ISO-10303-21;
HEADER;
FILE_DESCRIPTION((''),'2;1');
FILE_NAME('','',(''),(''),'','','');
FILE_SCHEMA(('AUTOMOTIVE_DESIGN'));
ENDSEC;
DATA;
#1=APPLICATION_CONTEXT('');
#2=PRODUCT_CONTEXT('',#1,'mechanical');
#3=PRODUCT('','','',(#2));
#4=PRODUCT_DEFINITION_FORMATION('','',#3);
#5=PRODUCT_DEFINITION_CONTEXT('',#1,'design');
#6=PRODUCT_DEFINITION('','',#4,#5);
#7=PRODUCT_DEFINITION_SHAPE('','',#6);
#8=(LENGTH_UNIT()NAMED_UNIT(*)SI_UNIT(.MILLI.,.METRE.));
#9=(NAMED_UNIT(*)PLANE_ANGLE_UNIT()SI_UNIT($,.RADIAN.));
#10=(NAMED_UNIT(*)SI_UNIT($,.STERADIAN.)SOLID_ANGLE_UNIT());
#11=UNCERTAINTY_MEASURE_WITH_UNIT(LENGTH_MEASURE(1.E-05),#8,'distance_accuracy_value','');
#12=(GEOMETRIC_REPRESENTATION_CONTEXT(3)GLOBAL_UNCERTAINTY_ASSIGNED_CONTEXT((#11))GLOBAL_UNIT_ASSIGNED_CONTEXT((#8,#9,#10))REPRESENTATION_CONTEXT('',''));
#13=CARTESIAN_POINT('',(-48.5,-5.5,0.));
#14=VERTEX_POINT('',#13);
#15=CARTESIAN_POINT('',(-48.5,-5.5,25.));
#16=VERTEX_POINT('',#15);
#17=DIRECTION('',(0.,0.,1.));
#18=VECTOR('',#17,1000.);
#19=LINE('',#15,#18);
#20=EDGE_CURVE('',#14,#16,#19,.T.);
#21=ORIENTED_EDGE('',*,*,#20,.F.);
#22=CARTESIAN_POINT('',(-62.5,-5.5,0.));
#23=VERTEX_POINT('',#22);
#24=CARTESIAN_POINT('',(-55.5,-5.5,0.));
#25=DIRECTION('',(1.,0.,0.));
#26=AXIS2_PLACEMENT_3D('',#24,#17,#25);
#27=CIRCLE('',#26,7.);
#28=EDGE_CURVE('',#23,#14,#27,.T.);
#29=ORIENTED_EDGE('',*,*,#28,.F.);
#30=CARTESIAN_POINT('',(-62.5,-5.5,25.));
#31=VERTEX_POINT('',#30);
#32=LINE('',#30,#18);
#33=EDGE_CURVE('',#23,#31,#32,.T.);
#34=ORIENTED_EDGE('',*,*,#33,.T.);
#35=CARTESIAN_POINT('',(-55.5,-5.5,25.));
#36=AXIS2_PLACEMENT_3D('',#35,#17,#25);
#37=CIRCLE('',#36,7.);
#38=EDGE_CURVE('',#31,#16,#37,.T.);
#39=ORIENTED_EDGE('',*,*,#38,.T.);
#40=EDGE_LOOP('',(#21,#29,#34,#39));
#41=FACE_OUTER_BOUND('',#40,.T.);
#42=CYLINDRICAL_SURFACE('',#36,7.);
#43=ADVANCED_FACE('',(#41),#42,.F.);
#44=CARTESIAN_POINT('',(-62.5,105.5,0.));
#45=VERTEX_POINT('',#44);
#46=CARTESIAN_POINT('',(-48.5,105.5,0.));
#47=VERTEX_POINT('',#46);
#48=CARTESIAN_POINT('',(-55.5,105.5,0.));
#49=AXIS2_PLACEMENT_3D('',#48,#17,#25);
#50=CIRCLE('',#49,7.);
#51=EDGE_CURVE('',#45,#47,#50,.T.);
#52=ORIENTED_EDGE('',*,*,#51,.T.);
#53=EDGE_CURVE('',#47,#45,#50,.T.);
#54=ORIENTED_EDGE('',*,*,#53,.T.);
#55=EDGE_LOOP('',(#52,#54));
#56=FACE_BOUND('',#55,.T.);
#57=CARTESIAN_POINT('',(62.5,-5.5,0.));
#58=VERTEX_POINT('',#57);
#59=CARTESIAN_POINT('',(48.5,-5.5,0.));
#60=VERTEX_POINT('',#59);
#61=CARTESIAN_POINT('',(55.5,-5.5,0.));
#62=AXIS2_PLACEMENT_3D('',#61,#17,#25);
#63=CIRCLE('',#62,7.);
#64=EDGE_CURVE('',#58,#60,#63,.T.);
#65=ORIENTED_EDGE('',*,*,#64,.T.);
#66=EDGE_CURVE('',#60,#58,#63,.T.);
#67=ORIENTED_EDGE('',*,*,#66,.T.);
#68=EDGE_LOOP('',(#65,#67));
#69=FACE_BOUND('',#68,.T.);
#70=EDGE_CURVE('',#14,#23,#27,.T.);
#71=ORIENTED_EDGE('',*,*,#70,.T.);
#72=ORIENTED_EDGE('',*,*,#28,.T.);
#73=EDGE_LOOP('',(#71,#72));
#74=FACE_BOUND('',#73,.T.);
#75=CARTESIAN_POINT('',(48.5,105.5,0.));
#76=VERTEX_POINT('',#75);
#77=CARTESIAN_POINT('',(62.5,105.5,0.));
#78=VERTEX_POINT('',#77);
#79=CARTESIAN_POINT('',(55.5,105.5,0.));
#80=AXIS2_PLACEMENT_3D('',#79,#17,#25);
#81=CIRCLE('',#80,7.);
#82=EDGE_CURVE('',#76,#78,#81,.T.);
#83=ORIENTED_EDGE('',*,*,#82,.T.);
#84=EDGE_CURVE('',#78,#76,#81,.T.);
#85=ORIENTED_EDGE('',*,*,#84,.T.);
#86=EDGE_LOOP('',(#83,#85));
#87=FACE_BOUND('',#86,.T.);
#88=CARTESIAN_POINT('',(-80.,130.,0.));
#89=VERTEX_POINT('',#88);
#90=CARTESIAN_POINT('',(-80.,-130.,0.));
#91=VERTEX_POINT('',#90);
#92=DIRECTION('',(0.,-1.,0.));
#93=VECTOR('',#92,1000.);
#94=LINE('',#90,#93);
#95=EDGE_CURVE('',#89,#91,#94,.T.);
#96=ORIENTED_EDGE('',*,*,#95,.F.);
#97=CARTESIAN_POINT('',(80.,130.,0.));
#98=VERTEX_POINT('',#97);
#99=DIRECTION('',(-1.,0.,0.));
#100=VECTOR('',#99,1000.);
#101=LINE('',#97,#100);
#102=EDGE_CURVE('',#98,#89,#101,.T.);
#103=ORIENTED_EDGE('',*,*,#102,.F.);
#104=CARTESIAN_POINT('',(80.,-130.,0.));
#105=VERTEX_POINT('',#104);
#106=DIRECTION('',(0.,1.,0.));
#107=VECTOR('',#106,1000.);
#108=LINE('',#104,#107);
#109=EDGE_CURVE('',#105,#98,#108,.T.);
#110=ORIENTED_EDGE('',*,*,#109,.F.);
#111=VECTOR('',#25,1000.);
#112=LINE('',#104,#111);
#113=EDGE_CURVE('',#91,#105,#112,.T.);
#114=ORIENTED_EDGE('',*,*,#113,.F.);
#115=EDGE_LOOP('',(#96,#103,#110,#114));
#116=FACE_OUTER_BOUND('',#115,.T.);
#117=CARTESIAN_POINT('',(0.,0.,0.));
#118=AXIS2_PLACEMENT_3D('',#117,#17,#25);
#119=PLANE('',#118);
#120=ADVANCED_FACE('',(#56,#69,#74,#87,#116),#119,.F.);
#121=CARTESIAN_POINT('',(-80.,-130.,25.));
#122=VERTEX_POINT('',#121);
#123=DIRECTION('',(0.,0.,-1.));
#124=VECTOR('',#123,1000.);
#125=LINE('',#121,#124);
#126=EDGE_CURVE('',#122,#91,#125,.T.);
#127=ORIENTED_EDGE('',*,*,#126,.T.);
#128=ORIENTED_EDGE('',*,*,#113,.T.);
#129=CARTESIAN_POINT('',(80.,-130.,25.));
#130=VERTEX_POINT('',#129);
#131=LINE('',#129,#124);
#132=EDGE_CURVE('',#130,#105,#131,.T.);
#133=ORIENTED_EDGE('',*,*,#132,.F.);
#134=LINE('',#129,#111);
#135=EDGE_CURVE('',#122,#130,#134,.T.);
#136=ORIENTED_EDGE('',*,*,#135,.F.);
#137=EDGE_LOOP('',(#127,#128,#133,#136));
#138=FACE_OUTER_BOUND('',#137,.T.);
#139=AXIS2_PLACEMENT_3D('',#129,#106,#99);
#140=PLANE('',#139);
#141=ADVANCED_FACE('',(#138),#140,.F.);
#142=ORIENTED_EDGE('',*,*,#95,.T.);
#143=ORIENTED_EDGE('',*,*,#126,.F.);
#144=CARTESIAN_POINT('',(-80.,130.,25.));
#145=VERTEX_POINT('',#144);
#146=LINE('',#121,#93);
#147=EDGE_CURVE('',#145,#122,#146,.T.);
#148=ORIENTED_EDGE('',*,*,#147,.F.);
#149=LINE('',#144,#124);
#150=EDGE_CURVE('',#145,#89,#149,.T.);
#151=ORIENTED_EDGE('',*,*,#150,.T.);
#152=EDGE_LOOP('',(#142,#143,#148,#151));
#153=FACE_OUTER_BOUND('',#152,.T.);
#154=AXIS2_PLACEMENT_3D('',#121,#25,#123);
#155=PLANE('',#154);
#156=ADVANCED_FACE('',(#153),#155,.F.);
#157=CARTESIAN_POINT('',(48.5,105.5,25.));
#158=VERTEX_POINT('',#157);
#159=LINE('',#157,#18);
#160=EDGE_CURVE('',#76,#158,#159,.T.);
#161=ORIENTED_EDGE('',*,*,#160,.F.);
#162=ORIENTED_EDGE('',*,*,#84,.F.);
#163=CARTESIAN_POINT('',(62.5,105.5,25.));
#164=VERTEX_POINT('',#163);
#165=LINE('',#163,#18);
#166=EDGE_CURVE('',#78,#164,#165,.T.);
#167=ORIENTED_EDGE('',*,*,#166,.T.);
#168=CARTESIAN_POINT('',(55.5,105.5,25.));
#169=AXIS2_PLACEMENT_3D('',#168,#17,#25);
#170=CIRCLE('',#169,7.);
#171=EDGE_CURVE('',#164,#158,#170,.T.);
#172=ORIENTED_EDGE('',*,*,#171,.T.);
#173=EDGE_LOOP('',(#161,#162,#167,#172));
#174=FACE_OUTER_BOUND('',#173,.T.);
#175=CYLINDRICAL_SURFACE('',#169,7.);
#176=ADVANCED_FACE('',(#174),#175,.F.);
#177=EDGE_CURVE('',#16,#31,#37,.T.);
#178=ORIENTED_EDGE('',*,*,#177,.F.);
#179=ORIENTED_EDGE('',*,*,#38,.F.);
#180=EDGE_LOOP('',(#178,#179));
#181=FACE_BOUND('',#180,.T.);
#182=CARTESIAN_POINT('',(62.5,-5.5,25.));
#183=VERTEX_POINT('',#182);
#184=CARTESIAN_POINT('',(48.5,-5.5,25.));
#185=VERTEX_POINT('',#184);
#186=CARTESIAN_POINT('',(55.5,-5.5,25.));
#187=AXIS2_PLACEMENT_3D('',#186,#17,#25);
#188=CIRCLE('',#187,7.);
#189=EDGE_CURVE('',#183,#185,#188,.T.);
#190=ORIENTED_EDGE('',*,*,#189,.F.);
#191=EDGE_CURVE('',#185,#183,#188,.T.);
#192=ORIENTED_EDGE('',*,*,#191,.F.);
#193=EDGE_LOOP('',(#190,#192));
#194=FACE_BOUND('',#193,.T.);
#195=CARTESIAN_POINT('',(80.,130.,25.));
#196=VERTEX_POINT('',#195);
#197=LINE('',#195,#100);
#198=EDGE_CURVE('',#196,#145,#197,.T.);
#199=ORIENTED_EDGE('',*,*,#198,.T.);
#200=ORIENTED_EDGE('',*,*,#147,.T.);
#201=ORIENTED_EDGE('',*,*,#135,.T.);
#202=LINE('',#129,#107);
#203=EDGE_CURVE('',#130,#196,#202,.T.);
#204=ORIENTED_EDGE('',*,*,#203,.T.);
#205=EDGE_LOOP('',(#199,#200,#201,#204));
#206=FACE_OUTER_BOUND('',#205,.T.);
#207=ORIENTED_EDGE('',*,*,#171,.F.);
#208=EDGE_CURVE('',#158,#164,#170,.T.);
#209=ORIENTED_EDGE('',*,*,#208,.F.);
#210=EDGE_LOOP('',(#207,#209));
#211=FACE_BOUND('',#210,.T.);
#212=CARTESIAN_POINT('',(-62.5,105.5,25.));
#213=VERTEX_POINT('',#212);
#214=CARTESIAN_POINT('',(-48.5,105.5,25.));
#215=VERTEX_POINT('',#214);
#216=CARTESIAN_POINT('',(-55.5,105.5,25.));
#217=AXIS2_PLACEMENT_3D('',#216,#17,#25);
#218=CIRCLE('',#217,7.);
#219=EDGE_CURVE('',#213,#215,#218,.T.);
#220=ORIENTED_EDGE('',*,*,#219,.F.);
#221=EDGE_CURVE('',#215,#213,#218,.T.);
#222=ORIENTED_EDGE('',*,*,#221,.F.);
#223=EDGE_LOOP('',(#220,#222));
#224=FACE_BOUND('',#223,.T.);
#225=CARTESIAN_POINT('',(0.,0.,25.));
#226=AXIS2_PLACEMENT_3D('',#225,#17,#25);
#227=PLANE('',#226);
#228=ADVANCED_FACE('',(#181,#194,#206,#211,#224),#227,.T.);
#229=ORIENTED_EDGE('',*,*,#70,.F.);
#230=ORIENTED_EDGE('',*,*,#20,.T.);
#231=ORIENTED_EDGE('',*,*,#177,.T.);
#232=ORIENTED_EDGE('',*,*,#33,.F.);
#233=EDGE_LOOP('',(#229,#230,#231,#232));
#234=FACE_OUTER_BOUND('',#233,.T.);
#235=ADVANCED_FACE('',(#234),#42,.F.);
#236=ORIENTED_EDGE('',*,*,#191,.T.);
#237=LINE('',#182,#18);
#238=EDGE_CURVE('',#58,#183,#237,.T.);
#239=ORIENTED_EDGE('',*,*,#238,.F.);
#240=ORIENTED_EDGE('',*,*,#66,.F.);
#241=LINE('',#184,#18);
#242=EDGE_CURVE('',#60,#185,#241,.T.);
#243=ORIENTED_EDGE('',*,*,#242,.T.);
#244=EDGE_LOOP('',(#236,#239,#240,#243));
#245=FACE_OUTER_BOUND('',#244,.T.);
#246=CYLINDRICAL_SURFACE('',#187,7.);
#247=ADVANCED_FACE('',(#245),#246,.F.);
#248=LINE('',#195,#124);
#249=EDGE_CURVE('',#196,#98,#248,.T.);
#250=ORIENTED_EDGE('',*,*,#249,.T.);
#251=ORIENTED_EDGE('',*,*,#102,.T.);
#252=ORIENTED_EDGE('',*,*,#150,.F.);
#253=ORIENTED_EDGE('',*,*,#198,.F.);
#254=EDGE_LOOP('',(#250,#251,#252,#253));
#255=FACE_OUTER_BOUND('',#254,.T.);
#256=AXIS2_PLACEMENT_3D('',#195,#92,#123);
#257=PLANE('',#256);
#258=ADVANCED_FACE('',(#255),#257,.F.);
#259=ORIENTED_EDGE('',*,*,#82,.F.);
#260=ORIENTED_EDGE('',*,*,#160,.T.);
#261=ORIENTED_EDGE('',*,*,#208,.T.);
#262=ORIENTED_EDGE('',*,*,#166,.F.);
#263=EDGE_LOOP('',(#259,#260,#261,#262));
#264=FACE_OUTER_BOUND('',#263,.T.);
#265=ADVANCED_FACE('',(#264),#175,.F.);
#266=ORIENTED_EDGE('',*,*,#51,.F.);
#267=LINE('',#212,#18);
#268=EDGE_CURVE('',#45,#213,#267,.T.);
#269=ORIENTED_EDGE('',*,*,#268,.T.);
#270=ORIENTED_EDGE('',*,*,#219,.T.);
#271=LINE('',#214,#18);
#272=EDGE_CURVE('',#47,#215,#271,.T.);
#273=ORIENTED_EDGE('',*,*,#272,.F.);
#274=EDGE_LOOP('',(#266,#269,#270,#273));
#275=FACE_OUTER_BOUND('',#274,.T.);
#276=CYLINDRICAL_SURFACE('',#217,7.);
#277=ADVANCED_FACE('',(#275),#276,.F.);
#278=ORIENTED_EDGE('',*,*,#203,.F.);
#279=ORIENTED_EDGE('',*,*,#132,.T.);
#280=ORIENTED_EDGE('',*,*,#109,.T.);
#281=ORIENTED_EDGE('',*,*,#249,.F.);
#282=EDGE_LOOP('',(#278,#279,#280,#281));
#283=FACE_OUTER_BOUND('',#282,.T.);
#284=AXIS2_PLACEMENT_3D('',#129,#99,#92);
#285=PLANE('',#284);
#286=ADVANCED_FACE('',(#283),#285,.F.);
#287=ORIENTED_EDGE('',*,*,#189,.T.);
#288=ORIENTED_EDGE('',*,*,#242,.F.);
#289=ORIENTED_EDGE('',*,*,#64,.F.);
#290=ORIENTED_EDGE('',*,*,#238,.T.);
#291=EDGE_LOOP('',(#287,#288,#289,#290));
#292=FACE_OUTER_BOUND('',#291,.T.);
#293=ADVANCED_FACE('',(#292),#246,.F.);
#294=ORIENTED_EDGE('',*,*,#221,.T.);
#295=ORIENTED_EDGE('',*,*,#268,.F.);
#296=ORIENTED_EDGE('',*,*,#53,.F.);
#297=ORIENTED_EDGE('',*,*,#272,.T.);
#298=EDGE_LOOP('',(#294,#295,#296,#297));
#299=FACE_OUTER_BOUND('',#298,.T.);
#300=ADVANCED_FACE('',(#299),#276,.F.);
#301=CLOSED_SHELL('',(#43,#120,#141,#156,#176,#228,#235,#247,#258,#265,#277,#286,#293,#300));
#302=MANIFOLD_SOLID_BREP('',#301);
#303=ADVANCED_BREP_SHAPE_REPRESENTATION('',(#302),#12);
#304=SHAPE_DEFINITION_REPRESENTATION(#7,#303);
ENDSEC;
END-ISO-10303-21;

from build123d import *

# Parameters (mm, degrees)
SKETCH_1_W          = 160
SKETCH_1_H          = 260
EXTRUDE_1_DEPTH     = 25
HOLE_WIZARD_M16_1_D = 14


with BuildPart() as part:
    # 草图1 → 凸台-拉伸1 (new body)
    with BuildSketch(Plane.XY):
        Rectangle(SKETCH_1_W, SKETCH_1_H)
    extrude(amount=EXTRUDE_1_DEPTH)

    # M16 螺纹孔1 (through all)
    with Locations(Plane.XY.offset(25)):
        with Locations((-55.5, 105.5), (-55.5, -5.5), (55.5, -5.5), (55.5, 105.5)):
            Hole(HOLE_WIZARD_M16_1_D / 2)


solid = part.part
